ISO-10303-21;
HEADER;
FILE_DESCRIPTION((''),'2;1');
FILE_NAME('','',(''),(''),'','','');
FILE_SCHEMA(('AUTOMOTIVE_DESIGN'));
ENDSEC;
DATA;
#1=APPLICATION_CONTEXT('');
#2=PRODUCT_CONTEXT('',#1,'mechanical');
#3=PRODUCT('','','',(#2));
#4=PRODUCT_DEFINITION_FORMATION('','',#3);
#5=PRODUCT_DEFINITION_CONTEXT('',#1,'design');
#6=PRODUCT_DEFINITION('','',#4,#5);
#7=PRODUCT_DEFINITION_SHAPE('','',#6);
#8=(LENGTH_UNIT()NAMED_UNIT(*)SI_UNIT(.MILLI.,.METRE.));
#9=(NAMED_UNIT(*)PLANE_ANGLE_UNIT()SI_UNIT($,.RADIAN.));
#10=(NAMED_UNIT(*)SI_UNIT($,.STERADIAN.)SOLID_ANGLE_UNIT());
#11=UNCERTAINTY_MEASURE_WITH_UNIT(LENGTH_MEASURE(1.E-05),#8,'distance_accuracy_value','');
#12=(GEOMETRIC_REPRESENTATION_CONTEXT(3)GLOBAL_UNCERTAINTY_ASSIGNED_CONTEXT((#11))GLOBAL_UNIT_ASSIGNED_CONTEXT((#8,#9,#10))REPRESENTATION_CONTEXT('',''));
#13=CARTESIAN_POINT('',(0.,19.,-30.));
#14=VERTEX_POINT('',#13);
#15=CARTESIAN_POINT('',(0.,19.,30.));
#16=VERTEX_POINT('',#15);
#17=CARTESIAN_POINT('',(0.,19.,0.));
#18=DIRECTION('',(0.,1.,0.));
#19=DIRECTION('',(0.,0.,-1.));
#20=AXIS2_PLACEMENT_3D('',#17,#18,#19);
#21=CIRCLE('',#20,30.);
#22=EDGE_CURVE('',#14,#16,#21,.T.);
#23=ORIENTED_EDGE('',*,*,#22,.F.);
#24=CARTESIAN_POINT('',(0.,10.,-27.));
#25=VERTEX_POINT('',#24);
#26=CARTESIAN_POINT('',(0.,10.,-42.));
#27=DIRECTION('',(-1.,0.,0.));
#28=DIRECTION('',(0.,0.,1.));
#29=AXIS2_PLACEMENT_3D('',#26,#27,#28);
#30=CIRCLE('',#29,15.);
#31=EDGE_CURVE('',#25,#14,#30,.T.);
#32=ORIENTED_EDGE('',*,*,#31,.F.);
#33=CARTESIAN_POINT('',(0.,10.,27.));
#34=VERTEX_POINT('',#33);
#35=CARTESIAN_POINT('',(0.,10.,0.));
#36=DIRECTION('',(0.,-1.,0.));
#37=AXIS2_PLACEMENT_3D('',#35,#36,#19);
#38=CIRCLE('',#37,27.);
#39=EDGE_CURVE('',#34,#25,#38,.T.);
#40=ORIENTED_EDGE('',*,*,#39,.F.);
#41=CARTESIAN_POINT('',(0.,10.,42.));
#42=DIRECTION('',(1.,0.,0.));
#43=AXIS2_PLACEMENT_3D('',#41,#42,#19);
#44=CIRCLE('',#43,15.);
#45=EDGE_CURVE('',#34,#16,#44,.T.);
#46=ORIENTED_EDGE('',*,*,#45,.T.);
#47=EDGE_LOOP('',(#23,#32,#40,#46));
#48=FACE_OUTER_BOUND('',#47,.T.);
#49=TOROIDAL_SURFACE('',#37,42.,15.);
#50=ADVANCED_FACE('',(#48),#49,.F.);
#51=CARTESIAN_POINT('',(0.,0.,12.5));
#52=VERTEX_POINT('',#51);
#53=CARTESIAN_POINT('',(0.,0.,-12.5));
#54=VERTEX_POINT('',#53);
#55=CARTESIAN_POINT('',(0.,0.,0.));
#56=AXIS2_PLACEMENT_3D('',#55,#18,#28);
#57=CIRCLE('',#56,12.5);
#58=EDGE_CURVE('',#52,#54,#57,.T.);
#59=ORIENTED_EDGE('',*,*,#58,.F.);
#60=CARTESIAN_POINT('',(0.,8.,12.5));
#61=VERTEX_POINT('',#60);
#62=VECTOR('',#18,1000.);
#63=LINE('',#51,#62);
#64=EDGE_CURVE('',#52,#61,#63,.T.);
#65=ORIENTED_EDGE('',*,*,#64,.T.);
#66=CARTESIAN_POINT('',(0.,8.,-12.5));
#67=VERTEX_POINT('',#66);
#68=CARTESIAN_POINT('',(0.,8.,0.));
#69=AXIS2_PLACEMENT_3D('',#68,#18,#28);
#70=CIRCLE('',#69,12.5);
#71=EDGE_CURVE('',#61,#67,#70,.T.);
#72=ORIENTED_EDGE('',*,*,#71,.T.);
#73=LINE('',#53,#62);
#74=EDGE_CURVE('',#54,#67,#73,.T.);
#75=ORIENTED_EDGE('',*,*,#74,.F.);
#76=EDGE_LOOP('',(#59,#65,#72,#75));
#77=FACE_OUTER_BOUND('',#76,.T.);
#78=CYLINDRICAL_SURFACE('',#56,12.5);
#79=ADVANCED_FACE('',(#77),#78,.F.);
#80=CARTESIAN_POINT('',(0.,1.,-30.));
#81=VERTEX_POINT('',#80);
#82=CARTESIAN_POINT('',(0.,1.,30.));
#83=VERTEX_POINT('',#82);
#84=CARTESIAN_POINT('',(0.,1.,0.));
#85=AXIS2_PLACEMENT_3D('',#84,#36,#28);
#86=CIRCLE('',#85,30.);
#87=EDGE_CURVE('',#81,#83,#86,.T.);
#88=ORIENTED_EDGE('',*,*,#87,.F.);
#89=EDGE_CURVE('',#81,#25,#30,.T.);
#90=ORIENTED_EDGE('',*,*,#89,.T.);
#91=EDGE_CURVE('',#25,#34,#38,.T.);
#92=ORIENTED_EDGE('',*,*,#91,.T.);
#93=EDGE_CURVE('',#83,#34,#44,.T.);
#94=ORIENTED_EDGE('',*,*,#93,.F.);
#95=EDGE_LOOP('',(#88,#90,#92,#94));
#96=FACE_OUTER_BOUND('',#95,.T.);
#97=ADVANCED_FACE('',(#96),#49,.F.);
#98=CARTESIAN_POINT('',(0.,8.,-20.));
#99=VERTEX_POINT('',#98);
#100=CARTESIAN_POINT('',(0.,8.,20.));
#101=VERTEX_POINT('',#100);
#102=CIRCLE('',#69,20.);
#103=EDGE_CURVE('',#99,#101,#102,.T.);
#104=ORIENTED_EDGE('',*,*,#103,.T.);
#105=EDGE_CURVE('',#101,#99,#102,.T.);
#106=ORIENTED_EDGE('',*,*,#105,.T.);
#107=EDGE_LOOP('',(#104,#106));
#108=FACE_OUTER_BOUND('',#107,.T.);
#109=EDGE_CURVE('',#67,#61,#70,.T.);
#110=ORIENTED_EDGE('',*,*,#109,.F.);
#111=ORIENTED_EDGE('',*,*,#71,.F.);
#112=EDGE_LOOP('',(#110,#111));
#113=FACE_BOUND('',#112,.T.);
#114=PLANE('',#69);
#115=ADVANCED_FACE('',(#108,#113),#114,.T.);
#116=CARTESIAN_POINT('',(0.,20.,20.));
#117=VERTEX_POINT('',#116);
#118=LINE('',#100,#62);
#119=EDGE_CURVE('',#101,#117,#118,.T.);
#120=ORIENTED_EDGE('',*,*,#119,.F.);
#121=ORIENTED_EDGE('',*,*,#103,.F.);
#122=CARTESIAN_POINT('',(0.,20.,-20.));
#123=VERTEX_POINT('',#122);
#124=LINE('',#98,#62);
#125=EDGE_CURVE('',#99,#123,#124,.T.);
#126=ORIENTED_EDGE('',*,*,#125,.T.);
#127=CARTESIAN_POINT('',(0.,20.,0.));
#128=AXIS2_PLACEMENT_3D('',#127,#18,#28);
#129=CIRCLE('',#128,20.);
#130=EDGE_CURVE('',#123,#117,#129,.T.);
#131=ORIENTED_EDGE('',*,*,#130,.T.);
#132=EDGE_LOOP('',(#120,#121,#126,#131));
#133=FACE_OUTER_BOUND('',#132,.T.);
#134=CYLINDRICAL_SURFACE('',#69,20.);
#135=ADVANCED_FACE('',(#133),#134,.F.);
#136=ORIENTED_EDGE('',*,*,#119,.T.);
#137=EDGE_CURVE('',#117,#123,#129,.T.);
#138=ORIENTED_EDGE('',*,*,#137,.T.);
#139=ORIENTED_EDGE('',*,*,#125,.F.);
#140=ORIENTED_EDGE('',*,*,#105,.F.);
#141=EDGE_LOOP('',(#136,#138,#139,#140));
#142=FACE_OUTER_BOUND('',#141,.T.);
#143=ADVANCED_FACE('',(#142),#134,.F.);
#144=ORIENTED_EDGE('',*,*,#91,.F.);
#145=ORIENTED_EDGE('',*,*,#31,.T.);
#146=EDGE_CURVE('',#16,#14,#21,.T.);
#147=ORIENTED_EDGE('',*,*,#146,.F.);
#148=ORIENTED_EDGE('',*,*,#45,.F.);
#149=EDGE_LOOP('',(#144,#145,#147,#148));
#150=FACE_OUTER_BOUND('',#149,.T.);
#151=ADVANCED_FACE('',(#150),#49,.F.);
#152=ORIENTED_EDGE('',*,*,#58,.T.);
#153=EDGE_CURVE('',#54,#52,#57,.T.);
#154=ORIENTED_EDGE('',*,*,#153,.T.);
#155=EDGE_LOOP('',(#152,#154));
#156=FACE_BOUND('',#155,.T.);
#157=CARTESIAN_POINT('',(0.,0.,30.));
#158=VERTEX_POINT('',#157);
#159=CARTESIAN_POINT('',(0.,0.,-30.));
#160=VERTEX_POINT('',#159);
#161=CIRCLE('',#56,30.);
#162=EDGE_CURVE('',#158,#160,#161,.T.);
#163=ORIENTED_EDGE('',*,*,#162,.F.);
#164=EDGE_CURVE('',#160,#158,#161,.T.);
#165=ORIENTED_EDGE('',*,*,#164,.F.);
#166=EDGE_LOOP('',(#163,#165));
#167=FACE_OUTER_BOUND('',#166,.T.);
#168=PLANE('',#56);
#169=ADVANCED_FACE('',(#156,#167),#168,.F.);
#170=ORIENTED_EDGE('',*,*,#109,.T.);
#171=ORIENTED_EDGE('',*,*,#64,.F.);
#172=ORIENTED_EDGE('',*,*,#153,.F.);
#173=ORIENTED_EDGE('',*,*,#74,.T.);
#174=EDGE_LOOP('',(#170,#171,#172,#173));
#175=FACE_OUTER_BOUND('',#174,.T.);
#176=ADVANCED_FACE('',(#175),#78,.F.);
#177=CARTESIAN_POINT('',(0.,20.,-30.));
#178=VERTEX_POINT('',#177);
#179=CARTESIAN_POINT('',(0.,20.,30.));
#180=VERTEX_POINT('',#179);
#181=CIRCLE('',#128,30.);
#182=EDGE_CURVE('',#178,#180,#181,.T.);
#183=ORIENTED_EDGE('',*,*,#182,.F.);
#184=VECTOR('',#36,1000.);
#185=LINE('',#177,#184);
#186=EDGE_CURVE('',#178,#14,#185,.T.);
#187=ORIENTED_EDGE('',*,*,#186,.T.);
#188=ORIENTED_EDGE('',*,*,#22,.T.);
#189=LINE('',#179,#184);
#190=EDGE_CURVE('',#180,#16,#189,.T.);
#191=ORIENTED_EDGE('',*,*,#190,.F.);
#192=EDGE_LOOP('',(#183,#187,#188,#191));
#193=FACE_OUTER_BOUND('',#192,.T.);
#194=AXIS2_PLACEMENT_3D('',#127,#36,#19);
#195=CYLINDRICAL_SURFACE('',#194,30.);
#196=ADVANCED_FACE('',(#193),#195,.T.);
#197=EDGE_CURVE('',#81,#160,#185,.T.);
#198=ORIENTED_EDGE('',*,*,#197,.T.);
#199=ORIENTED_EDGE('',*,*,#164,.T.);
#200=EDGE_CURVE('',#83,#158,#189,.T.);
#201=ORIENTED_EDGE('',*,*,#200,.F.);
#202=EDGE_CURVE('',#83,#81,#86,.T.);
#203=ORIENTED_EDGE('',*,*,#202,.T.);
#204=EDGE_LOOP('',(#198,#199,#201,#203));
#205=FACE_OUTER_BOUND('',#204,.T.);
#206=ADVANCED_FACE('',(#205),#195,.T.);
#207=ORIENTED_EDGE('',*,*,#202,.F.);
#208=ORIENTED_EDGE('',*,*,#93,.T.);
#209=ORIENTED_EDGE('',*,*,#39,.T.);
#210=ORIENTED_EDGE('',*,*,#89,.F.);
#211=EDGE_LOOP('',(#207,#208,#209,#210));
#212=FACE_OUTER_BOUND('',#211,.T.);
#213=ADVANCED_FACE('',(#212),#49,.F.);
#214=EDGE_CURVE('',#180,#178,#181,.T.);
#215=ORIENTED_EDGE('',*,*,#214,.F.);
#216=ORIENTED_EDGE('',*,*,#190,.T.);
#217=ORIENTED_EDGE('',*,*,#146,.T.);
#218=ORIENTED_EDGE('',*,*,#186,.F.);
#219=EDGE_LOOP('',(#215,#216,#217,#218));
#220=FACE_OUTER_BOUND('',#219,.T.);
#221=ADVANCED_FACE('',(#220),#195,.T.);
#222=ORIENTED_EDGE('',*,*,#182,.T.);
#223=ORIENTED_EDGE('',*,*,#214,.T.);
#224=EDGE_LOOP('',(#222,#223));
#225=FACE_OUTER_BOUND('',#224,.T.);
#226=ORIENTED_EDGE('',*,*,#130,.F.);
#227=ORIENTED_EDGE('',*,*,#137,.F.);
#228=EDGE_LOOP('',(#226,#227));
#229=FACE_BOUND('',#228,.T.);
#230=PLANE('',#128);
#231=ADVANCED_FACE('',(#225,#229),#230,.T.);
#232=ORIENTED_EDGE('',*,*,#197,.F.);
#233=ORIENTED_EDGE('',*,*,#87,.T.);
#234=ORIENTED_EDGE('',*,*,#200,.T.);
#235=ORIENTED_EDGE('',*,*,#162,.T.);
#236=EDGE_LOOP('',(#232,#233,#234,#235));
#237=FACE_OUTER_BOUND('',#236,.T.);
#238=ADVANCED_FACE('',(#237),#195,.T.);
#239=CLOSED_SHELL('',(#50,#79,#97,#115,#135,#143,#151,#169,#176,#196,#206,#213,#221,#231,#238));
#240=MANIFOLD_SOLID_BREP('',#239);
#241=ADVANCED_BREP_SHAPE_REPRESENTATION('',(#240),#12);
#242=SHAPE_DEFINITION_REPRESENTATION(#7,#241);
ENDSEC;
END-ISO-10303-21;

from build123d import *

# Parameters (mm, degrees)
SKETCH_1_R               = 30
EXTRUDE_1_DEPTH          = 20
SKETCH_2_R               = 20
CUT_EXTRUDE_1_DEPTH      = 12
CUT_EXTRUDE_2_DEPTH      = 45.09081537
CUT_EXTRUDE_2_DEPTH_BACK = 45.09081537
SKETCH_4_R               = 12.5
SKETCH_5_R               = 15


with BuildPart() as part:
    # 草图1 → 凸台-拉伸1 (new body)
    with BuildSketch(Plane(origin=(0, 0, 0), x_dir=(1, 0, 0), z_dir=(0, 1, 0))):
        with Locations(Location((0, 0, 0), (0, 0, 270))):
            Circle(SKETCH_1_R)
    extrude(amount=EXTRUDE_1_DEPTH)

    # 草图2 → 切除-拉伸1 (cut)
    with BuildSketch(Plane(origin=(0, 20, 0), x_dir=(1, 0, 0), z_dir=(0, 1, 0))):
        with Locations(Location((0, 0, 0), (0, 0, 270))):
            Circle(SKETCH_2_R)
    extrude(amount=-CUT_EXTRUDE_1_DEPTH, mode=Mode.SUBTRACT)

    # 草图4 → 切除-拉伸2 (cut, two sides: drawn at the far end of the back side and taken through both)
    with BuildSketch(Plane(origin=(0, 8, 0), x_dir=(1, 0, 0), z_dir=(0, 1, 0)).offset(-CUT_EXTRUDE_2_DEPTH_BACK)):
        with Locations(Location((0, 0, 0), (0, 0, 270))):
            Circle(SKETCH_4_R)
    extrude(amount=CUT_EXTRUDE_2_DEPTH + CUT_EXTRUDE_2_DEPTH_BACK, mode=Mode.SUBTRACT)

    # 草图5 → 切除-旋转1 (revolve, cut)
    with BuildSketch(Plane.XY, mode=Mode.PRIVATE) as cut_revolve_1_sk:
        with Locations((42, 10)):
            Circle(SKETCH_5_R)
    revolve(cut_revolve_1_sk.sketch.rotate(Axis((0, 0, 0), (0, 1, 0)), 90), axis=Axis((0, 0, 0), (0, 1, 0)), mode=Mode.SUBTRACT)


solid = part.part
